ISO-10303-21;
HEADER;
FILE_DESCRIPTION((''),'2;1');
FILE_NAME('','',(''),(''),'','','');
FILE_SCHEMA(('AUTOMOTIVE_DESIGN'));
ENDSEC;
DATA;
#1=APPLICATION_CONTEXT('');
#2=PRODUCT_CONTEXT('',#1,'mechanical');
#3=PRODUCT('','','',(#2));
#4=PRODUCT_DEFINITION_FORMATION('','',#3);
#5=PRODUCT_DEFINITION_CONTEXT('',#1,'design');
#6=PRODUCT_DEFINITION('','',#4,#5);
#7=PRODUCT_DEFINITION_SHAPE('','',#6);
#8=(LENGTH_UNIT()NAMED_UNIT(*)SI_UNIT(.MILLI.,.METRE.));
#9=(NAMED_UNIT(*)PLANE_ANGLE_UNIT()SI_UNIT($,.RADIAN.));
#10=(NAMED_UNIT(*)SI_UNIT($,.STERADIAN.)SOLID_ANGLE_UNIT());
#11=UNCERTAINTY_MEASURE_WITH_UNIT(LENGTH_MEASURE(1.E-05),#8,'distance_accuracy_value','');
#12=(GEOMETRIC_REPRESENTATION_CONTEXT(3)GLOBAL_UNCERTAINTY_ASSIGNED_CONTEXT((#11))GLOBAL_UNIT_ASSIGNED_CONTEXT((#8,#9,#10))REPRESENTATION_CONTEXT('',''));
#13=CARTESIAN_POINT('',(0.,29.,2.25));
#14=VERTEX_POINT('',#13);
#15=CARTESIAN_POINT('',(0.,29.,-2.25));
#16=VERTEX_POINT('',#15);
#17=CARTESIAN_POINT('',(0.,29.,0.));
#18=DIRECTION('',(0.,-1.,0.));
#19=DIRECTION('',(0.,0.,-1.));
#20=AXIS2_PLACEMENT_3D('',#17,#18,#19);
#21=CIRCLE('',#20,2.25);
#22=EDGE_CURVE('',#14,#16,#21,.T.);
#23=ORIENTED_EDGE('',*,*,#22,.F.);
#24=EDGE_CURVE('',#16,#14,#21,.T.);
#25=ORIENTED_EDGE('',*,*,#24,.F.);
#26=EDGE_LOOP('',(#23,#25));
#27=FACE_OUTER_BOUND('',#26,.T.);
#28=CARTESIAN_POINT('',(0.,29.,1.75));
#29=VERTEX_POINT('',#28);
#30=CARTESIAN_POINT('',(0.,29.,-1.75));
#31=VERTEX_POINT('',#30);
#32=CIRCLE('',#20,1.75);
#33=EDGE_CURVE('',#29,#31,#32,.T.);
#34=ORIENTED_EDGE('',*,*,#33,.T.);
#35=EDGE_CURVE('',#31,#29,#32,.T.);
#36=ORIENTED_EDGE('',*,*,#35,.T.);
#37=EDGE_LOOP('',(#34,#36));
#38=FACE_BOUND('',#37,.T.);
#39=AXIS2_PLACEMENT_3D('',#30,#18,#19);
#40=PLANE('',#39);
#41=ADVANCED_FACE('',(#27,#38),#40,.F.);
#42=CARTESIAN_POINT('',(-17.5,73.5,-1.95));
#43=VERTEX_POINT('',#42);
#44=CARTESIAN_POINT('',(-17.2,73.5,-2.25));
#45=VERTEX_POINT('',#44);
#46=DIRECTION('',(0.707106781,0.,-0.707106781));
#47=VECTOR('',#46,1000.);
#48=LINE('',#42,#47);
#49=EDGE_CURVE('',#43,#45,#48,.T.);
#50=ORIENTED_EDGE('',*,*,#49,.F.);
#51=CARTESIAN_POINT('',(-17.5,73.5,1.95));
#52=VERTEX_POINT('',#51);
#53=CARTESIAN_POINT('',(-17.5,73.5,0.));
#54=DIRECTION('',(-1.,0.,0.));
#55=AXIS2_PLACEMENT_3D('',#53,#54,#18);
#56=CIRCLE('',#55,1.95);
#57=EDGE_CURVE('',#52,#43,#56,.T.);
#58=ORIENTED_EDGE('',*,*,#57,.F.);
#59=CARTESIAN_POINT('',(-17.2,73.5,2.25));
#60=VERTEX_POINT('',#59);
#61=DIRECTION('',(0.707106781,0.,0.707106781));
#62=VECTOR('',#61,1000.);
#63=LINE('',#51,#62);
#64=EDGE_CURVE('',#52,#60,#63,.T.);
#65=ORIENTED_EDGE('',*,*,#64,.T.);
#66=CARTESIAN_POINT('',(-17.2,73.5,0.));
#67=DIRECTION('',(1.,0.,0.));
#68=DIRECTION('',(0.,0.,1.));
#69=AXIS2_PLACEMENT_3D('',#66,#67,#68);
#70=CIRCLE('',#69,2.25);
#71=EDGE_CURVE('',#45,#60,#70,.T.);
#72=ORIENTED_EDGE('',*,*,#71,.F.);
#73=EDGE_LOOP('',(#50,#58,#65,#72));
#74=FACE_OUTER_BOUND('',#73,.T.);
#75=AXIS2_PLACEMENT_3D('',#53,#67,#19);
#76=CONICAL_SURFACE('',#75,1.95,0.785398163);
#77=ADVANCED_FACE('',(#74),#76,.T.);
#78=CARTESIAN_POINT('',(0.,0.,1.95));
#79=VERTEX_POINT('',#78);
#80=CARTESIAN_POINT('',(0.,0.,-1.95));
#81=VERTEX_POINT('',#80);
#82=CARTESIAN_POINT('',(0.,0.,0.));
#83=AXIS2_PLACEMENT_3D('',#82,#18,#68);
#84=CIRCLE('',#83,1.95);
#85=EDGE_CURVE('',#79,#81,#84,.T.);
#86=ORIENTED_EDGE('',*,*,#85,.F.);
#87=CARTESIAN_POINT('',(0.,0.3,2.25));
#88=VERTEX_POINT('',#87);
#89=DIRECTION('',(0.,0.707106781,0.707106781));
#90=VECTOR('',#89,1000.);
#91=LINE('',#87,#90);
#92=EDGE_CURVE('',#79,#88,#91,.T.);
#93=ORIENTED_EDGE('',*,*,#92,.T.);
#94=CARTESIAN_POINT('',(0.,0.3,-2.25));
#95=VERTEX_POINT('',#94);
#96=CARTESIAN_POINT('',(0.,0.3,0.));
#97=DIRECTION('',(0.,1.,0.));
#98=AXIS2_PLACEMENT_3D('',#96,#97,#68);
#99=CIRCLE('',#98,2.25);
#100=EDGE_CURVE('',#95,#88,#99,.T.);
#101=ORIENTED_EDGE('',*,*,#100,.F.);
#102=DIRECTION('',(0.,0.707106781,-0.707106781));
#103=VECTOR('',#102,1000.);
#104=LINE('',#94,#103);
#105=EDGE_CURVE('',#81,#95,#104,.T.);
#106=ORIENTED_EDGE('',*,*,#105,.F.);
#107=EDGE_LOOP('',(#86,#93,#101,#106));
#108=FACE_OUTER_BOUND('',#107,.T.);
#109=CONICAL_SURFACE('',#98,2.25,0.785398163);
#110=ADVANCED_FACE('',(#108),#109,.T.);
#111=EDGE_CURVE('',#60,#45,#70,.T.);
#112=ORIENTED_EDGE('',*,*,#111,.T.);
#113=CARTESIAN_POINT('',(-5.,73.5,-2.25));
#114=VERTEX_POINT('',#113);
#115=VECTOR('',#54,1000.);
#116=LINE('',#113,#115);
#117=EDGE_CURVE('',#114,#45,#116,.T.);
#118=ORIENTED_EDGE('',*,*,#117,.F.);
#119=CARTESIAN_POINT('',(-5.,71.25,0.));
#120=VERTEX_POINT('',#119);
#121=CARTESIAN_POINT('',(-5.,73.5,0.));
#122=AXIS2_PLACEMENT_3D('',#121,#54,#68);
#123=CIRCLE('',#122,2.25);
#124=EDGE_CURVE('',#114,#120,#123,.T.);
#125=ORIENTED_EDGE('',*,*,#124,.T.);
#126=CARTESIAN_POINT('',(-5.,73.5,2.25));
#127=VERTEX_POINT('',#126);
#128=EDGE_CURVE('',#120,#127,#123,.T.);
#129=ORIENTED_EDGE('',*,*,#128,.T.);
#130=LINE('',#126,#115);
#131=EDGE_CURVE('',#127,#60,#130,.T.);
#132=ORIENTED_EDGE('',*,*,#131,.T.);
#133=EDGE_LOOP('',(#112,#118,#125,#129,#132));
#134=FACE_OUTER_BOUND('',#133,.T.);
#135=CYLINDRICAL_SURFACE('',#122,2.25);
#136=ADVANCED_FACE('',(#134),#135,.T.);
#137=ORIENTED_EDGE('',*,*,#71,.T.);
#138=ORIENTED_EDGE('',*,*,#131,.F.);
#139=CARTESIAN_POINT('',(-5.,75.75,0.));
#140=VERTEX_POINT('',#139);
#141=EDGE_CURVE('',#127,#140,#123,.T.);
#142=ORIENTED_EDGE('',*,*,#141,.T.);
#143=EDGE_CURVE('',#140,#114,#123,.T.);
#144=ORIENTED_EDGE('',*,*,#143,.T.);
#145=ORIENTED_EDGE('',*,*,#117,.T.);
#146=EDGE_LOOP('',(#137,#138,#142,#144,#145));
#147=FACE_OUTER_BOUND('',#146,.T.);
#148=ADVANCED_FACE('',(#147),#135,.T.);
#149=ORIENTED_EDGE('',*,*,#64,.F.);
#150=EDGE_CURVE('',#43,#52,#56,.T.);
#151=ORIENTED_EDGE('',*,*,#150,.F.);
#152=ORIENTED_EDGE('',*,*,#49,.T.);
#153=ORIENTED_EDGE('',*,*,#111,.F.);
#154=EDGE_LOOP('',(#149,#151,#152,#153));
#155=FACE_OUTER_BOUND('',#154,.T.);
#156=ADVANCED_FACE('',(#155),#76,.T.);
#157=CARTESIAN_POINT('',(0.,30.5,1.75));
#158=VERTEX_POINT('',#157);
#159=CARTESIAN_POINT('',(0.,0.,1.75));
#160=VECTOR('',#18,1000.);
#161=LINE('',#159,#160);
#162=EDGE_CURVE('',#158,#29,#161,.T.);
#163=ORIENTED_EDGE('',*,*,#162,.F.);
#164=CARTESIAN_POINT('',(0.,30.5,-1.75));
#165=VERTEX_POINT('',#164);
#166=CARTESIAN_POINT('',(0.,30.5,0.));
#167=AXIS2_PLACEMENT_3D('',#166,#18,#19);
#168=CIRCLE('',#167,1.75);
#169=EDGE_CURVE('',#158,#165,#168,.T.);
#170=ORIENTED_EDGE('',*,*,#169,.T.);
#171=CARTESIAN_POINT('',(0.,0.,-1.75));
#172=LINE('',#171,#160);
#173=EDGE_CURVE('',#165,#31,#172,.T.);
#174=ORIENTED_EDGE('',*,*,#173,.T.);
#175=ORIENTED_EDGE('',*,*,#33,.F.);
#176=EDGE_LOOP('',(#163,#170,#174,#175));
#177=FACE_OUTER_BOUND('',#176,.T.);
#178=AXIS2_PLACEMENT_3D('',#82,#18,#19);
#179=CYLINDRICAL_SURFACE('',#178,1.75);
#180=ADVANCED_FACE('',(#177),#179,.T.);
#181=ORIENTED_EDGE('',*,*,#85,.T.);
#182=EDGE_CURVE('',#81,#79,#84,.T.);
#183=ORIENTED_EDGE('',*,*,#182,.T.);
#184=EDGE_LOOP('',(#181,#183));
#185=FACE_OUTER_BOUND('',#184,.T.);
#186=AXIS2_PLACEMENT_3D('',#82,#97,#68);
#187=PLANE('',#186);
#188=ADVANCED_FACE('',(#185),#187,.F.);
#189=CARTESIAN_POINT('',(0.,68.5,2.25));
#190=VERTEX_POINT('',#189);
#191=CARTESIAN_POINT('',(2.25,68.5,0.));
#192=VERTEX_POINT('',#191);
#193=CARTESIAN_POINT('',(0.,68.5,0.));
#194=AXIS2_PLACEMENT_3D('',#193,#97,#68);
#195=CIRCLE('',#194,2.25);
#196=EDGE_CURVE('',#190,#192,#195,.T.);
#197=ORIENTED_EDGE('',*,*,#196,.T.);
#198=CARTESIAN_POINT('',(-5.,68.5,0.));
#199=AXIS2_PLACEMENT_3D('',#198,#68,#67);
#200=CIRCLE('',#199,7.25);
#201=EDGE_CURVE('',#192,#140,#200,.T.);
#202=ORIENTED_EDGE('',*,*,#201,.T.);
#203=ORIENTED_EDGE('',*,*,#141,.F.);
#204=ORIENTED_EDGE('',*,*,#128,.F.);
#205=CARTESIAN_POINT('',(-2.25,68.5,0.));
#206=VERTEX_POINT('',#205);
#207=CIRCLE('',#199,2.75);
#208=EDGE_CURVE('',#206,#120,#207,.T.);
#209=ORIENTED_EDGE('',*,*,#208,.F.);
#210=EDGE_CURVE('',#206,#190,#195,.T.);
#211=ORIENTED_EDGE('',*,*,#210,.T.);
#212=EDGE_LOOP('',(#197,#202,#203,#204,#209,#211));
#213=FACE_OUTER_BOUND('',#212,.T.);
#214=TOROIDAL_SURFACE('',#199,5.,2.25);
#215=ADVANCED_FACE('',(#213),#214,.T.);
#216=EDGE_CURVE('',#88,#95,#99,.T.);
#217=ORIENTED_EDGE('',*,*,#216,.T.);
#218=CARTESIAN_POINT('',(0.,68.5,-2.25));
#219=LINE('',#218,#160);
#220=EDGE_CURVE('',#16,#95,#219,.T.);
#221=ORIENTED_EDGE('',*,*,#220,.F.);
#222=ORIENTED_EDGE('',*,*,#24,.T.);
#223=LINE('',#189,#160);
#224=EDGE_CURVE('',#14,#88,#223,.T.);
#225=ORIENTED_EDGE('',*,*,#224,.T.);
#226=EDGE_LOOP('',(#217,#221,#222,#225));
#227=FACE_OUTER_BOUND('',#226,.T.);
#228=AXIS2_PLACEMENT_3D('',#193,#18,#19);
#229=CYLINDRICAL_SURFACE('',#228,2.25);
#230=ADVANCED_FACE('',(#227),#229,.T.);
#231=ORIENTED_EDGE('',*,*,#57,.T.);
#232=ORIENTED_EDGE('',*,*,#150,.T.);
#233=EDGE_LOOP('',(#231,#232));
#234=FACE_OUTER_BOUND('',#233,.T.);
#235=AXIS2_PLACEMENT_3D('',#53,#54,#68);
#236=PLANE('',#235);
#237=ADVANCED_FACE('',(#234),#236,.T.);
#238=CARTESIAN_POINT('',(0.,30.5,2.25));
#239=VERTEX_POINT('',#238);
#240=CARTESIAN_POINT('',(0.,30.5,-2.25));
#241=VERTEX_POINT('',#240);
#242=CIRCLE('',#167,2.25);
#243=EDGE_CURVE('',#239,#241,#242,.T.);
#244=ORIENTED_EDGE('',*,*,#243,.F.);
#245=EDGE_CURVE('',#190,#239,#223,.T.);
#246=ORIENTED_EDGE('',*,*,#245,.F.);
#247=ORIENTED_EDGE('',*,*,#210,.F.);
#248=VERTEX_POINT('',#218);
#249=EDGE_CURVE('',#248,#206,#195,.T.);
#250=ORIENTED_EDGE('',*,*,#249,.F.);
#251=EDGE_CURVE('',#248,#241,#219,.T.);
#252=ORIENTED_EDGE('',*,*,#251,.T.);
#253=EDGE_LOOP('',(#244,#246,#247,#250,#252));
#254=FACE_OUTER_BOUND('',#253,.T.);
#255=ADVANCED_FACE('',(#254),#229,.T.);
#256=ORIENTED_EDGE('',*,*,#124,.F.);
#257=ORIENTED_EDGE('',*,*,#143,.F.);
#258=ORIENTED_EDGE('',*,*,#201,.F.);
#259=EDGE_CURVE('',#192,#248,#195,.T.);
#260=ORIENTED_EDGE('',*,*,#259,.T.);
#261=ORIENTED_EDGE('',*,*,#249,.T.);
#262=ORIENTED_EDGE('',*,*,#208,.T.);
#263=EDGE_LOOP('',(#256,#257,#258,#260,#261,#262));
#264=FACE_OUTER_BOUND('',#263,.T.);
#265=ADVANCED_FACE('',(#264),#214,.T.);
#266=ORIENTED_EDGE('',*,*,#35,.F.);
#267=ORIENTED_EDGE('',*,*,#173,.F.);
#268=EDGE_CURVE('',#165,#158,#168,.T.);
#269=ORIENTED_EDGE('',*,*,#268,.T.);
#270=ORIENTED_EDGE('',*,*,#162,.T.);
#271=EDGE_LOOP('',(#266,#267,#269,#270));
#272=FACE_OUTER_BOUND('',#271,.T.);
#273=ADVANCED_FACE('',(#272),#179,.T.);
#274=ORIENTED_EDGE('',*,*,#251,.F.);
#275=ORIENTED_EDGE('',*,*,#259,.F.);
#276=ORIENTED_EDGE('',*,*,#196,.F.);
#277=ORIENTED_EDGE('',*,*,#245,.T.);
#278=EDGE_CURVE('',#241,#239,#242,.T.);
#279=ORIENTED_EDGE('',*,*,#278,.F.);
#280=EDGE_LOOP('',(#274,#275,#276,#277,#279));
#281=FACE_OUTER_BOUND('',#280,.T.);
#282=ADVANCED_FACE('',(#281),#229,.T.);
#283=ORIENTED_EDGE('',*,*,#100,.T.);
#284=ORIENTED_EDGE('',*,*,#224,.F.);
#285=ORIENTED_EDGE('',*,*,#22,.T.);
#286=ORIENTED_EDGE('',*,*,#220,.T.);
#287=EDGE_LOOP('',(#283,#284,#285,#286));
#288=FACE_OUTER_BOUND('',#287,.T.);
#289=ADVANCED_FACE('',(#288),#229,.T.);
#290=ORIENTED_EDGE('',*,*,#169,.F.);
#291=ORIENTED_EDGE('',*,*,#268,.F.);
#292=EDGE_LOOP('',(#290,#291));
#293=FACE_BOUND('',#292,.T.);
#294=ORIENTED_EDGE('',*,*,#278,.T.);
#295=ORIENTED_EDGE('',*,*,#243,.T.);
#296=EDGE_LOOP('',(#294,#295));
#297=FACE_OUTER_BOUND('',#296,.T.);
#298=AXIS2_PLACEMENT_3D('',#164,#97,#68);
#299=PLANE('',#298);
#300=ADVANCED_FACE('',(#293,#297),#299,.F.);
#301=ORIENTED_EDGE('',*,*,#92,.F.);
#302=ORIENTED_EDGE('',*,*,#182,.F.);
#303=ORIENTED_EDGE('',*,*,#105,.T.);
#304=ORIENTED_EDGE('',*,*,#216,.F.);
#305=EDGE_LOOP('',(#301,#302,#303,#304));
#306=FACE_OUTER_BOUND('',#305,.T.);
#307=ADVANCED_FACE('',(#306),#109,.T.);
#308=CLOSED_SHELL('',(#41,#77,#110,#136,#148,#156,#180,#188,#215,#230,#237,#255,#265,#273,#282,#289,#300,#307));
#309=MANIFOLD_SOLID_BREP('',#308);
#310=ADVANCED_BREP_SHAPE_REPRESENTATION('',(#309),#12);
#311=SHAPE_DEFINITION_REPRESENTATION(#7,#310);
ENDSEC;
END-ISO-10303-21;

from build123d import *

# Parameters (mm, degrees)
SKETCH2_R     = 2.25
SKETCH3_W     = 0.5
SKETCH3_H     = 1.5
CHAMFER1_SIZE = 0.3


with BuildPart() as part:
    # Sweep1: sweep along a path in Sketch1
    with BuildLine(Plane.XY) as sweep1_path:
        Line((0, 0), (0, 68.5))
        ThreePointArc((0, 68.5), (-1.464466094, 72.035533906), (-5, 73.5))
        Line((-5, 73.5), (-17.5, 73.5))
    # Sketch2 → Sweep1 (sweep)
    with BuildSketch(Plane(origin=(0, 0, 0), x_dir=(1, 0, 0), z_dir=(0, 1, 0))):
        Circle(SKETCH2_R)
    sweep(path=sweep1_path.line)

    # Sketch3 → Cut-Revolve1 (revolve, cut)
    with BuildSketch(Plane(origin=(0, 0, 0), x_dir=(0, 0, -1), z_dir=(1, 0, 0))):
        with Locations((2, 29.75)):
            Rectangle(SKETCH3_W, SKETCH3_H)
    revolve(axis=Axis((0, 0, 0), (0, 1, 0)), mode=Mode.SUBTRACT)

    # Chamfer1
    chamfer1_edges = [part.edges().sort_by_distance(p)[0] for p in [
        (-2.25, 0, 0),
        (-17.5, 71.25, 0),
    ]]
    chamfer(chamfer1_edges, length=CHAMFER1_SIZE)


solid = part.part
